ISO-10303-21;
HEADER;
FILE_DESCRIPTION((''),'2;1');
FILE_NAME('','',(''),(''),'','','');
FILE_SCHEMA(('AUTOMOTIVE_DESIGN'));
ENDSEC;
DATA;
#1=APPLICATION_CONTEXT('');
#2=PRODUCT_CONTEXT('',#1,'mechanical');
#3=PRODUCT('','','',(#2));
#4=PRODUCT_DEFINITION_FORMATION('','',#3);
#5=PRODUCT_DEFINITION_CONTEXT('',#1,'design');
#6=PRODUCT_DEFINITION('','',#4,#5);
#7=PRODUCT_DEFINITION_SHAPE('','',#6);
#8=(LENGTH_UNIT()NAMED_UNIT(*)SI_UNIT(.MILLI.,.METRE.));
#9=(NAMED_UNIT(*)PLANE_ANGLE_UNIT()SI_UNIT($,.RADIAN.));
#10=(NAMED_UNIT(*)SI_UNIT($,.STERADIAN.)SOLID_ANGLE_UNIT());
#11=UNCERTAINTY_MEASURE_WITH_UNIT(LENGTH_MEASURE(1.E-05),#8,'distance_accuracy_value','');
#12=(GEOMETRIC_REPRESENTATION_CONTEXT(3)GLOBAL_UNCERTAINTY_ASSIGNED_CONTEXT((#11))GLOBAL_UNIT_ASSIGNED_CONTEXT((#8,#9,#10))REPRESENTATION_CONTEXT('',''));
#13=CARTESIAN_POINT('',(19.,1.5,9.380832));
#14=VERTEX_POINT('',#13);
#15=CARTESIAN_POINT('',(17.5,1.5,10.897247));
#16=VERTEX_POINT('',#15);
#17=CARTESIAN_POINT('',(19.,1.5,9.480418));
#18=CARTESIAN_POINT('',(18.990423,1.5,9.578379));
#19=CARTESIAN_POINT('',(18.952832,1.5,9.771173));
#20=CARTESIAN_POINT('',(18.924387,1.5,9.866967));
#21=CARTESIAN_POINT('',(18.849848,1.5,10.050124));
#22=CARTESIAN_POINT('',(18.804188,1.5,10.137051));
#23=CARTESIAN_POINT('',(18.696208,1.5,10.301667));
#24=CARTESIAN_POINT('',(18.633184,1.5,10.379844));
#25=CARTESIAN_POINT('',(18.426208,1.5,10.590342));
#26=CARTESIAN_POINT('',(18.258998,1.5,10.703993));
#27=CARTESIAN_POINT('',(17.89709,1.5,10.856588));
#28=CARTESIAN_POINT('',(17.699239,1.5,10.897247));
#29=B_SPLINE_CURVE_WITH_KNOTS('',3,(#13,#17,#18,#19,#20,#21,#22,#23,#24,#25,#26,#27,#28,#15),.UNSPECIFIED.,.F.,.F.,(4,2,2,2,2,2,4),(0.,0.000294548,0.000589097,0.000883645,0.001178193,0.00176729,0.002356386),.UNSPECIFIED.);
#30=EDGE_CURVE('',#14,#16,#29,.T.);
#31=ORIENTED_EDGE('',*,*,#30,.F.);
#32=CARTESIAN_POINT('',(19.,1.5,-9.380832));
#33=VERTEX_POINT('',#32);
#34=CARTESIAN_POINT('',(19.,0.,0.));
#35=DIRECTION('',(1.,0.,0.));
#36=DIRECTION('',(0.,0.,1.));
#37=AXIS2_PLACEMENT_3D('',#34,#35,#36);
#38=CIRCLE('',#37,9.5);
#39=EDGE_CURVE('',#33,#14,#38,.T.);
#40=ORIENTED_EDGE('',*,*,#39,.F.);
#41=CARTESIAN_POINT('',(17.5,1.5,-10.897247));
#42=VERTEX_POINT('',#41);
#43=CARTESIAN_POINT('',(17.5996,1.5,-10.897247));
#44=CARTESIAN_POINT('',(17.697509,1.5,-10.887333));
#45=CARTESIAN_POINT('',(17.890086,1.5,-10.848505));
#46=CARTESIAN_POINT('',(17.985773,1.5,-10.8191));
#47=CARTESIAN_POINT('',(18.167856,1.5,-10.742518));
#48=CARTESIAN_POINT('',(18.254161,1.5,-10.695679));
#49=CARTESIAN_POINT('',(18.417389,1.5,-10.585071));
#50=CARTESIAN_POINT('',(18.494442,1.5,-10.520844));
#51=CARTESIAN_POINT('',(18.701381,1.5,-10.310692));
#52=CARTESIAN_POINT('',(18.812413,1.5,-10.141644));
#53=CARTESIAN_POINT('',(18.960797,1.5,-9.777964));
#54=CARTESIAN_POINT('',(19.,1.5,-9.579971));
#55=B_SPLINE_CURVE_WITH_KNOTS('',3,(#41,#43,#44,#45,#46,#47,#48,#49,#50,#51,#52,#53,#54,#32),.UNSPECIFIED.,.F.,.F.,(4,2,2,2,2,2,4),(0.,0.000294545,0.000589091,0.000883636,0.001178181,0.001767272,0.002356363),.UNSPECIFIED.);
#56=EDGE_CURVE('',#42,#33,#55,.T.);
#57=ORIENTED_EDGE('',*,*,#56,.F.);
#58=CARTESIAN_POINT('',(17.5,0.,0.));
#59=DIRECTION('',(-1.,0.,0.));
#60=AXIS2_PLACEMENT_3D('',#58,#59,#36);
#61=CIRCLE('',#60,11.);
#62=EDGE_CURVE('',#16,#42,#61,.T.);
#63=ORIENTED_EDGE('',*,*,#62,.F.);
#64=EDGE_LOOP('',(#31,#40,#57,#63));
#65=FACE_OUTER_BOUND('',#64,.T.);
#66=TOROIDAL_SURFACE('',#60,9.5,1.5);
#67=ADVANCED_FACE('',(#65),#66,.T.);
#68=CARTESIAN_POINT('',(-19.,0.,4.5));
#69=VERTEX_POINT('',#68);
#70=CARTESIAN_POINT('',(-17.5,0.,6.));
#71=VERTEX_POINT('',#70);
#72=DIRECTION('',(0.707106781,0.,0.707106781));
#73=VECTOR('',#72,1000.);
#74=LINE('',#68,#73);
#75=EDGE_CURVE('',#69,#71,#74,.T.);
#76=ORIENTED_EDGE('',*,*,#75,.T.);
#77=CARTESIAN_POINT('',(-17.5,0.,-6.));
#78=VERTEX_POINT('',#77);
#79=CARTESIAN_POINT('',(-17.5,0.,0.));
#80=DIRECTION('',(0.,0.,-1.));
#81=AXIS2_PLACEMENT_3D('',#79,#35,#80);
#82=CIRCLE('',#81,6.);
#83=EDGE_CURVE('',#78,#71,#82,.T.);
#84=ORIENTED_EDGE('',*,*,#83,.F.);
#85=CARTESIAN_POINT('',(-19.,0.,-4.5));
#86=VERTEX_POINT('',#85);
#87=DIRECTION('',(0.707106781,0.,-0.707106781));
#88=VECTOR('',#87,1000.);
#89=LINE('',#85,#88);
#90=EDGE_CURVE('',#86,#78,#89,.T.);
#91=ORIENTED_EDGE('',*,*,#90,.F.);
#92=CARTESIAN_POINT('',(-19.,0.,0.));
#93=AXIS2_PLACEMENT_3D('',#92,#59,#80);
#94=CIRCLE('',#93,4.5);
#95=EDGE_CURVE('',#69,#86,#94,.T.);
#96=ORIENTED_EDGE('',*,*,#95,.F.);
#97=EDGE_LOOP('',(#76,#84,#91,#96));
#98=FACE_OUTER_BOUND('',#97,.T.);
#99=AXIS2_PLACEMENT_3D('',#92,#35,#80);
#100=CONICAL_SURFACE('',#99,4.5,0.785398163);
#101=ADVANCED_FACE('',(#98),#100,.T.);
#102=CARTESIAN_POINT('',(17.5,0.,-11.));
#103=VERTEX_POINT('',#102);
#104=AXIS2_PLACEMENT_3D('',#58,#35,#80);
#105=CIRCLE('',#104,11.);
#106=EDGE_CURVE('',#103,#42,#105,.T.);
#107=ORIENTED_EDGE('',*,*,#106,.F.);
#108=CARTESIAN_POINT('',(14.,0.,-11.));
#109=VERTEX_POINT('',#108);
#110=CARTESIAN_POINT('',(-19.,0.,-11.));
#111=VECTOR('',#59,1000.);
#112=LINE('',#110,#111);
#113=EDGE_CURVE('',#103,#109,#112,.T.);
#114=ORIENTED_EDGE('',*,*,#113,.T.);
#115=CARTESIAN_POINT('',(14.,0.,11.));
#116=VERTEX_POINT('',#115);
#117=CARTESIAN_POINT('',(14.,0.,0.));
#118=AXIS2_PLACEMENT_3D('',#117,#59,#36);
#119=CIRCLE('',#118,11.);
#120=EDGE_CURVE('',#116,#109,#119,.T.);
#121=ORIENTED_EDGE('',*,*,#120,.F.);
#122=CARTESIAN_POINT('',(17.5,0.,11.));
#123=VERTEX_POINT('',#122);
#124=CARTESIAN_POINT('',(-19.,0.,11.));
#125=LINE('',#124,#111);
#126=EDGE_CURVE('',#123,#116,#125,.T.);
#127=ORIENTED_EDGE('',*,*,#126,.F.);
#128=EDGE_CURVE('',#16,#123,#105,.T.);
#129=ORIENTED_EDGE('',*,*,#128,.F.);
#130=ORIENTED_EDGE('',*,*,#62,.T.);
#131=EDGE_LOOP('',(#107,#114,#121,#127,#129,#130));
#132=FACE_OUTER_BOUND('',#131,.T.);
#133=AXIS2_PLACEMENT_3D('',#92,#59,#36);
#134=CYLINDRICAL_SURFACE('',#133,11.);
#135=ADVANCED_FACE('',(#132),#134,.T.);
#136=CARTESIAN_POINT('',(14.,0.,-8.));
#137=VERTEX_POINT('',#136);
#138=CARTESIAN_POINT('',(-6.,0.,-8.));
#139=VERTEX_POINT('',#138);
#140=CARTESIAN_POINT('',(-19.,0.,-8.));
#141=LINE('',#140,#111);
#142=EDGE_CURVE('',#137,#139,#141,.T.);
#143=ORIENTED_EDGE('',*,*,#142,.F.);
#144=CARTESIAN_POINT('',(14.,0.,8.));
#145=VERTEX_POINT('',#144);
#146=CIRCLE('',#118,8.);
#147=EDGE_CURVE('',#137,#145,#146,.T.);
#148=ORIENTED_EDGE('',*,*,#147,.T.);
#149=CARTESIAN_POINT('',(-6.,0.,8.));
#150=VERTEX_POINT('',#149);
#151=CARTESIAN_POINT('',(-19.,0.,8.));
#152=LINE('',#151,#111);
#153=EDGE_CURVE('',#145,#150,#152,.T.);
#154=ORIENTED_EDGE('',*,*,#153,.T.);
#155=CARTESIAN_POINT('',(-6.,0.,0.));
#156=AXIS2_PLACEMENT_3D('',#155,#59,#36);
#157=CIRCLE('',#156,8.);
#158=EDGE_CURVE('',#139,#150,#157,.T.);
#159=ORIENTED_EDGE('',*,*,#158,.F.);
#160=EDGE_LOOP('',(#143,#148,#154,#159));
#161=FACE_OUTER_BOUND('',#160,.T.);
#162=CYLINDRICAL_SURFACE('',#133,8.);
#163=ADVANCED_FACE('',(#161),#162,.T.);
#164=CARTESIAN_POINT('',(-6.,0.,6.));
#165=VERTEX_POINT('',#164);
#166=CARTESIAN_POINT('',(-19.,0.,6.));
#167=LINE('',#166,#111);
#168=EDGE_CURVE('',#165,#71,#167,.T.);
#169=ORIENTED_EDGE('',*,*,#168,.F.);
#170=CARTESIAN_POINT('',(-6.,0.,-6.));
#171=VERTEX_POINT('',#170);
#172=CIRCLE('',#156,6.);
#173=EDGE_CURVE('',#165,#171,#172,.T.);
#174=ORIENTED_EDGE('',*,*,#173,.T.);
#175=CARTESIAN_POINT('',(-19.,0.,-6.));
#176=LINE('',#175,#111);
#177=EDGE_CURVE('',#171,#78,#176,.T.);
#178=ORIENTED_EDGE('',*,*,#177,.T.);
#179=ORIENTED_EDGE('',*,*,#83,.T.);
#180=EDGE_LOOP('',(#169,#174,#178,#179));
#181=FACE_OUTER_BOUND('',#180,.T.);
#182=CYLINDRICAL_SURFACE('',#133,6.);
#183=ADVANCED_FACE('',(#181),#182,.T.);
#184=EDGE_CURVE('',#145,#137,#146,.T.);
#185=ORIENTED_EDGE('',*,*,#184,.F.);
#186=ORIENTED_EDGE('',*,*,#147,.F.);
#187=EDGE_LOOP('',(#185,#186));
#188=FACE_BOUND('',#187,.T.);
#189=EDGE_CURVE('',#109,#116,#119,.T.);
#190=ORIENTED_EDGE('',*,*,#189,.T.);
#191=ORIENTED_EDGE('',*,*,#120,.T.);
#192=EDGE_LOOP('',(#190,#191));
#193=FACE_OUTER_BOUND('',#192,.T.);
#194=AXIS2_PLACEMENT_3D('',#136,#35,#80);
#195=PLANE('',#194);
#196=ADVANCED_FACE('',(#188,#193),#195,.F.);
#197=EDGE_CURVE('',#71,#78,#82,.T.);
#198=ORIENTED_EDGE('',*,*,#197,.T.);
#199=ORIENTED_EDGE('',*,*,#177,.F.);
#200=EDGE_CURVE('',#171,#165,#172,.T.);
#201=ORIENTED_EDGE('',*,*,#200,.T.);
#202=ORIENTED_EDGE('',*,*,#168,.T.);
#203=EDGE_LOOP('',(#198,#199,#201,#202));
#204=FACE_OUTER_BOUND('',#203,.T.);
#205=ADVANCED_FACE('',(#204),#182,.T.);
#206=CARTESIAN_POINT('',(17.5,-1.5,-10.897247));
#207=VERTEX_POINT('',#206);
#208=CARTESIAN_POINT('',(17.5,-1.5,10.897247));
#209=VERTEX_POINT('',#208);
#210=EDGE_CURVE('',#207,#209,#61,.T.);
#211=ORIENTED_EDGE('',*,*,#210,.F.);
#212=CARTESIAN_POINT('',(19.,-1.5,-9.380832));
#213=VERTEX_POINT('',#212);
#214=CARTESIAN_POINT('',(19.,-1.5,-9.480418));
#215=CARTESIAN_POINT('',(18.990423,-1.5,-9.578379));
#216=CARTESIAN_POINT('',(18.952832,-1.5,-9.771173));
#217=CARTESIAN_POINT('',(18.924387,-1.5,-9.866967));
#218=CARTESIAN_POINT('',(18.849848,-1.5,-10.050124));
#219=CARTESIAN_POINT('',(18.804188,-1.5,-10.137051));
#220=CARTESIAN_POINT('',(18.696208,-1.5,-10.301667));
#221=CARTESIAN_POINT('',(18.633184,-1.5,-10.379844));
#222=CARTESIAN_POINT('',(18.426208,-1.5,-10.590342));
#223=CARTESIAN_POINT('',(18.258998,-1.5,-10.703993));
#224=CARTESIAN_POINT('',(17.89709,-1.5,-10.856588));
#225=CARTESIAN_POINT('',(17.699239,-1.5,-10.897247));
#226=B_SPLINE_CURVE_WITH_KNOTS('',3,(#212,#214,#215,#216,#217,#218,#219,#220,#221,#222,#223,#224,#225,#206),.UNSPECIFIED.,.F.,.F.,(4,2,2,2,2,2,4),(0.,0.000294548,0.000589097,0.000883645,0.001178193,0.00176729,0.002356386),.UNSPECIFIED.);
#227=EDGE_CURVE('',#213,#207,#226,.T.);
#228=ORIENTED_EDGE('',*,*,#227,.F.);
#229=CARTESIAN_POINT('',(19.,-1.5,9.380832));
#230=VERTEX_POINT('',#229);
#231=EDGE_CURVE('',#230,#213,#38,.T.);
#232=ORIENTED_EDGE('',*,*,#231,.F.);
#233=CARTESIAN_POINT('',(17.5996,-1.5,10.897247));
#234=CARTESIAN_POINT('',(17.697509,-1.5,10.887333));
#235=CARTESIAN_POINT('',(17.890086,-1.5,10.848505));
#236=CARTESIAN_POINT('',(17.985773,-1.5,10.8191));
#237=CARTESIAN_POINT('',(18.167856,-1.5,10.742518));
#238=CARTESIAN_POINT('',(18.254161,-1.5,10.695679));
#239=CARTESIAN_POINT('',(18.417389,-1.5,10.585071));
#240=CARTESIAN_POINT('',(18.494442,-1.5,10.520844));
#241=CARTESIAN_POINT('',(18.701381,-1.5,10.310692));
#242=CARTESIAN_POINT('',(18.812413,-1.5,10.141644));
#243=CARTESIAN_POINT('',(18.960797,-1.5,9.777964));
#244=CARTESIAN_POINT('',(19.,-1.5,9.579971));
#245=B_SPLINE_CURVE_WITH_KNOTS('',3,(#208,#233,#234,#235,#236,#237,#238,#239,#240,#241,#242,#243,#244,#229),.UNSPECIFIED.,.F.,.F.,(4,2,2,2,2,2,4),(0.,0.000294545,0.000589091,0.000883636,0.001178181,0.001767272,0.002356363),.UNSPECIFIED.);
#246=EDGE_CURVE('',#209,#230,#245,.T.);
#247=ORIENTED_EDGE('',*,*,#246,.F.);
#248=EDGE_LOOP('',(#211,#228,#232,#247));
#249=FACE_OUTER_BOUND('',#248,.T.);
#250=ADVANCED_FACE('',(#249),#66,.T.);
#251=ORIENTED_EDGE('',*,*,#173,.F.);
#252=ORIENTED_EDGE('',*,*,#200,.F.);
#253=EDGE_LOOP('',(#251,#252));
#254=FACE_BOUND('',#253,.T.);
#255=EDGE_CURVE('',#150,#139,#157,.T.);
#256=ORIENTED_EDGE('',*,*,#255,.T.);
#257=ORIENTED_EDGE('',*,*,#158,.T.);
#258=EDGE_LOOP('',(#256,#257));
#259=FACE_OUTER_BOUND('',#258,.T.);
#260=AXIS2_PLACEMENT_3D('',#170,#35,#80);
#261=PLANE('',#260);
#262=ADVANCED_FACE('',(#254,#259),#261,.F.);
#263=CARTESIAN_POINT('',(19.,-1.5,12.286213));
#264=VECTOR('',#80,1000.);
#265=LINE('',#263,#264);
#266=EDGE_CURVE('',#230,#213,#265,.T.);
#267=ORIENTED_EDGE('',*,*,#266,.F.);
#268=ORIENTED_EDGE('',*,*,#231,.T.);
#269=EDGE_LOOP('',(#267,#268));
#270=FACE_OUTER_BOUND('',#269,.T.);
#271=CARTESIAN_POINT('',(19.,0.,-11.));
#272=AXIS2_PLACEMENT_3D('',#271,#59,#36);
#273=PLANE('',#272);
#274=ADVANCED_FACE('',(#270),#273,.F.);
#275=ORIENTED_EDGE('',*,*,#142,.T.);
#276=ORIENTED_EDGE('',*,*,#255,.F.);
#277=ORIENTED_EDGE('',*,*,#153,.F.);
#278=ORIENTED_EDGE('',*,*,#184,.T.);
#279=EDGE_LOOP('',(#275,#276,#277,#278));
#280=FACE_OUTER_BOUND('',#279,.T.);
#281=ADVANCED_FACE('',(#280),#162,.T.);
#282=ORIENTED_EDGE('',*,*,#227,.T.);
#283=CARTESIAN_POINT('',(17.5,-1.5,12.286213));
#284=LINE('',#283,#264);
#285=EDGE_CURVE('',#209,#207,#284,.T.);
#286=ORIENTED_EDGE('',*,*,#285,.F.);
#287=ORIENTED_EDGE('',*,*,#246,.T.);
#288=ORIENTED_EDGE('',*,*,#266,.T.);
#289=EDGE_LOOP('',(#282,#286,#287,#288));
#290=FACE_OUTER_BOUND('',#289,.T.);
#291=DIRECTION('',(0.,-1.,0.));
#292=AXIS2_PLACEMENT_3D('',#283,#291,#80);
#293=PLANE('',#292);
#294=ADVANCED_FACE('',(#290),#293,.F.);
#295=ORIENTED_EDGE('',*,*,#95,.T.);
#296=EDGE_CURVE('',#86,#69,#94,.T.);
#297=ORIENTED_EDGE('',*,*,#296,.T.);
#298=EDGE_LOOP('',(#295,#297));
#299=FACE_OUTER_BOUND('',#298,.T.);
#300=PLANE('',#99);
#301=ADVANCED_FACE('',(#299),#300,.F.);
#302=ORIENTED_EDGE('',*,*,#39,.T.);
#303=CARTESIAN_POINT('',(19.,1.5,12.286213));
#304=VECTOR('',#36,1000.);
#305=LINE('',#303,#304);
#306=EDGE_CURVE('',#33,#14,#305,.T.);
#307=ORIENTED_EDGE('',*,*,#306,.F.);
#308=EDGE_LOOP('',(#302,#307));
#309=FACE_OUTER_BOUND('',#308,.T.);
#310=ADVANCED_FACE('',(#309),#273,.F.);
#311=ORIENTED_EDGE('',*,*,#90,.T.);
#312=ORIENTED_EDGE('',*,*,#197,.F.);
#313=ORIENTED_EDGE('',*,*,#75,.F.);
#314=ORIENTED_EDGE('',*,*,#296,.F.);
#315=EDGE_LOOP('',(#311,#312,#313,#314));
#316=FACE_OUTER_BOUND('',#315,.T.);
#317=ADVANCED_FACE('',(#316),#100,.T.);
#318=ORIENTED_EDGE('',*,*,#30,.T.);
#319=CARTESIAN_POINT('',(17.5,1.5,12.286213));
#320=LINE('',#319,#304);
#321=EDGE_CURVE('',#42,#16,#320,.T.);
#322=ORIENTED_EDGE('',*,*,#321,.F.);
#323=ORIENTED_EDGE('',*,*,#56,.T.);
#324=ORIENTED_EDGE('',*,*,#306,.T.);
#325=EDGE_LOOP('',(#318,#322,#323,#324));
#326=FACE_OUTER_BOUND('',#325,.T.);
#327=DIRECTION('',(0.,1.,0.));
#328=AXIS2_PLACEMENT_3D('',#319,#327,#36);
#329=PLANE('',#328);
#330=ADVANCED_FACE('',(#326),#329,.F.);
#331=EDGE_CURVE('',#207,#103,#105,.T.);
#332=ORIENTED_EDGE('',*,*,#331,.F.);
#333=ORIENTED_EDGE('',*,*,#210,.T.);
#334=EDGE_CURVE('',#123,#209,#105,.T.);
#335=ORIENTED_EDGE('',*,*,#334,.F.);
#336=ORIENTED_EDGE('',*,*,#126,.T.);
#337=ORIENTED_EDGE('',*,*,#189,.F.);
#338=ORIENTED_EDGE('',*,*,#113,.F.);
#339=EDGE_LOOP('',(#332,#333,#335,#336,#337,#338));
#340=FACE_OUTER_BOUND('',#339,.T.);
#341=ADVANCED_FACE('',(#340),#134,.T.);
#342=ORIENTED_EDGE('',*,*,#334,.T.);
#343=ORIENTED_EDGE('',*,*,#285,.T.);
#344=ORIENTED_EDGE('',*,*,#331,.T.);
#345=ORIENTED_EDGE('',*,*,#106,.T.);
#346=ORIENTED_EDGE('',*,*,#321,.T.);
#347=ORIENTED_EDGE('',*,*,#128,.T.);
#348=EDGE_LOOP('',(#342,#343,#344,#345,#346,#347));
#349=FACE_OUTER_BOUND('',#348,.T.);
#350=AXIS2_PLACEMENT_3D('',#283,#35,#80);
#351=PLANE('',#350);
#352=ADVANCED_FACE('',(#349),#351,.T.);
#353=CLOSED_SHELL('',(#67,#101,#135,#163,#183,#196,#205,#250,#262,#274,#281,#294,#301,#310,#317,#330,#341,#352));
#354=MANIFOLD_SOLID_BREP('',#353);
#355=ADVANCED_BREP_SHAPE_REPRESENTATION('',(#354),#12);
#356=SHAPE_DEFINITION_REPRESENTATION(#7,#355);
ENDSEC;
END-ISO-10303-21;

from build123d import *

# Parameters (mm, degrees)
SKETCH2_W          = 26.278844289
SKETCH2_H          = 3
CUT_EXTRUDE1_DEPTH = 1.5
FILLET1_R          = 1.5
CHAMFER1_SIZE      = 1.5


with BuildPart() as part:
    # Sketch1 → Revolve1 (revolve)
    with BuildSketch(Plane(origin=(0, 0, 0), x_dir=(1, 0, 0), z_dir=(0, 1, 0)), mode=Mode.PRIVATE) as revolve1_sk:
        Polygon((-19, 0), (-19, 6), (-6, 6), (-6, 8), (14, 8), (14, 11), (19, 11), (19, 0), align=None)
    revolve(revolve1_sk.sketch.rotate(Axis((-19, 0, 0), (1, 0, 0)), 180), axis=Axis((-19, 0, 0), (1, 0, 0)))

    # Sketch2 → Cut-Extrude1 (cut)
    with BuildSketch(Plane(origin=(19, 0, 0), x_dir=(0, 0, -1), z_dir=(1, 0, 0))):
        with Locations((0.853209231, 0)):
            Rectangle(SKETCH2_W, SKETCH2_H)
    extrude(amount=-CUT_EXTRUDE1_DEPTH, mode=Mode.SUBTRACT)

    # Fillet1
    fillet1_edges = [part.edges().sort_by_distance(p)[0] for p in [
        (19, -11, 0),
        (19, 11, 0),
    ]]
    fillet(fillet1_edges, radius=FILLET1_R)

    # Chamfer1
    chamfer1_edges = [part.edges().sort_by_distance(p)[0] for p in [
        (-19, 0, -6),
    ]]
    chamfer(chamfer1_edges, length=CHAMFER1_SIZE)


solid = part.part
